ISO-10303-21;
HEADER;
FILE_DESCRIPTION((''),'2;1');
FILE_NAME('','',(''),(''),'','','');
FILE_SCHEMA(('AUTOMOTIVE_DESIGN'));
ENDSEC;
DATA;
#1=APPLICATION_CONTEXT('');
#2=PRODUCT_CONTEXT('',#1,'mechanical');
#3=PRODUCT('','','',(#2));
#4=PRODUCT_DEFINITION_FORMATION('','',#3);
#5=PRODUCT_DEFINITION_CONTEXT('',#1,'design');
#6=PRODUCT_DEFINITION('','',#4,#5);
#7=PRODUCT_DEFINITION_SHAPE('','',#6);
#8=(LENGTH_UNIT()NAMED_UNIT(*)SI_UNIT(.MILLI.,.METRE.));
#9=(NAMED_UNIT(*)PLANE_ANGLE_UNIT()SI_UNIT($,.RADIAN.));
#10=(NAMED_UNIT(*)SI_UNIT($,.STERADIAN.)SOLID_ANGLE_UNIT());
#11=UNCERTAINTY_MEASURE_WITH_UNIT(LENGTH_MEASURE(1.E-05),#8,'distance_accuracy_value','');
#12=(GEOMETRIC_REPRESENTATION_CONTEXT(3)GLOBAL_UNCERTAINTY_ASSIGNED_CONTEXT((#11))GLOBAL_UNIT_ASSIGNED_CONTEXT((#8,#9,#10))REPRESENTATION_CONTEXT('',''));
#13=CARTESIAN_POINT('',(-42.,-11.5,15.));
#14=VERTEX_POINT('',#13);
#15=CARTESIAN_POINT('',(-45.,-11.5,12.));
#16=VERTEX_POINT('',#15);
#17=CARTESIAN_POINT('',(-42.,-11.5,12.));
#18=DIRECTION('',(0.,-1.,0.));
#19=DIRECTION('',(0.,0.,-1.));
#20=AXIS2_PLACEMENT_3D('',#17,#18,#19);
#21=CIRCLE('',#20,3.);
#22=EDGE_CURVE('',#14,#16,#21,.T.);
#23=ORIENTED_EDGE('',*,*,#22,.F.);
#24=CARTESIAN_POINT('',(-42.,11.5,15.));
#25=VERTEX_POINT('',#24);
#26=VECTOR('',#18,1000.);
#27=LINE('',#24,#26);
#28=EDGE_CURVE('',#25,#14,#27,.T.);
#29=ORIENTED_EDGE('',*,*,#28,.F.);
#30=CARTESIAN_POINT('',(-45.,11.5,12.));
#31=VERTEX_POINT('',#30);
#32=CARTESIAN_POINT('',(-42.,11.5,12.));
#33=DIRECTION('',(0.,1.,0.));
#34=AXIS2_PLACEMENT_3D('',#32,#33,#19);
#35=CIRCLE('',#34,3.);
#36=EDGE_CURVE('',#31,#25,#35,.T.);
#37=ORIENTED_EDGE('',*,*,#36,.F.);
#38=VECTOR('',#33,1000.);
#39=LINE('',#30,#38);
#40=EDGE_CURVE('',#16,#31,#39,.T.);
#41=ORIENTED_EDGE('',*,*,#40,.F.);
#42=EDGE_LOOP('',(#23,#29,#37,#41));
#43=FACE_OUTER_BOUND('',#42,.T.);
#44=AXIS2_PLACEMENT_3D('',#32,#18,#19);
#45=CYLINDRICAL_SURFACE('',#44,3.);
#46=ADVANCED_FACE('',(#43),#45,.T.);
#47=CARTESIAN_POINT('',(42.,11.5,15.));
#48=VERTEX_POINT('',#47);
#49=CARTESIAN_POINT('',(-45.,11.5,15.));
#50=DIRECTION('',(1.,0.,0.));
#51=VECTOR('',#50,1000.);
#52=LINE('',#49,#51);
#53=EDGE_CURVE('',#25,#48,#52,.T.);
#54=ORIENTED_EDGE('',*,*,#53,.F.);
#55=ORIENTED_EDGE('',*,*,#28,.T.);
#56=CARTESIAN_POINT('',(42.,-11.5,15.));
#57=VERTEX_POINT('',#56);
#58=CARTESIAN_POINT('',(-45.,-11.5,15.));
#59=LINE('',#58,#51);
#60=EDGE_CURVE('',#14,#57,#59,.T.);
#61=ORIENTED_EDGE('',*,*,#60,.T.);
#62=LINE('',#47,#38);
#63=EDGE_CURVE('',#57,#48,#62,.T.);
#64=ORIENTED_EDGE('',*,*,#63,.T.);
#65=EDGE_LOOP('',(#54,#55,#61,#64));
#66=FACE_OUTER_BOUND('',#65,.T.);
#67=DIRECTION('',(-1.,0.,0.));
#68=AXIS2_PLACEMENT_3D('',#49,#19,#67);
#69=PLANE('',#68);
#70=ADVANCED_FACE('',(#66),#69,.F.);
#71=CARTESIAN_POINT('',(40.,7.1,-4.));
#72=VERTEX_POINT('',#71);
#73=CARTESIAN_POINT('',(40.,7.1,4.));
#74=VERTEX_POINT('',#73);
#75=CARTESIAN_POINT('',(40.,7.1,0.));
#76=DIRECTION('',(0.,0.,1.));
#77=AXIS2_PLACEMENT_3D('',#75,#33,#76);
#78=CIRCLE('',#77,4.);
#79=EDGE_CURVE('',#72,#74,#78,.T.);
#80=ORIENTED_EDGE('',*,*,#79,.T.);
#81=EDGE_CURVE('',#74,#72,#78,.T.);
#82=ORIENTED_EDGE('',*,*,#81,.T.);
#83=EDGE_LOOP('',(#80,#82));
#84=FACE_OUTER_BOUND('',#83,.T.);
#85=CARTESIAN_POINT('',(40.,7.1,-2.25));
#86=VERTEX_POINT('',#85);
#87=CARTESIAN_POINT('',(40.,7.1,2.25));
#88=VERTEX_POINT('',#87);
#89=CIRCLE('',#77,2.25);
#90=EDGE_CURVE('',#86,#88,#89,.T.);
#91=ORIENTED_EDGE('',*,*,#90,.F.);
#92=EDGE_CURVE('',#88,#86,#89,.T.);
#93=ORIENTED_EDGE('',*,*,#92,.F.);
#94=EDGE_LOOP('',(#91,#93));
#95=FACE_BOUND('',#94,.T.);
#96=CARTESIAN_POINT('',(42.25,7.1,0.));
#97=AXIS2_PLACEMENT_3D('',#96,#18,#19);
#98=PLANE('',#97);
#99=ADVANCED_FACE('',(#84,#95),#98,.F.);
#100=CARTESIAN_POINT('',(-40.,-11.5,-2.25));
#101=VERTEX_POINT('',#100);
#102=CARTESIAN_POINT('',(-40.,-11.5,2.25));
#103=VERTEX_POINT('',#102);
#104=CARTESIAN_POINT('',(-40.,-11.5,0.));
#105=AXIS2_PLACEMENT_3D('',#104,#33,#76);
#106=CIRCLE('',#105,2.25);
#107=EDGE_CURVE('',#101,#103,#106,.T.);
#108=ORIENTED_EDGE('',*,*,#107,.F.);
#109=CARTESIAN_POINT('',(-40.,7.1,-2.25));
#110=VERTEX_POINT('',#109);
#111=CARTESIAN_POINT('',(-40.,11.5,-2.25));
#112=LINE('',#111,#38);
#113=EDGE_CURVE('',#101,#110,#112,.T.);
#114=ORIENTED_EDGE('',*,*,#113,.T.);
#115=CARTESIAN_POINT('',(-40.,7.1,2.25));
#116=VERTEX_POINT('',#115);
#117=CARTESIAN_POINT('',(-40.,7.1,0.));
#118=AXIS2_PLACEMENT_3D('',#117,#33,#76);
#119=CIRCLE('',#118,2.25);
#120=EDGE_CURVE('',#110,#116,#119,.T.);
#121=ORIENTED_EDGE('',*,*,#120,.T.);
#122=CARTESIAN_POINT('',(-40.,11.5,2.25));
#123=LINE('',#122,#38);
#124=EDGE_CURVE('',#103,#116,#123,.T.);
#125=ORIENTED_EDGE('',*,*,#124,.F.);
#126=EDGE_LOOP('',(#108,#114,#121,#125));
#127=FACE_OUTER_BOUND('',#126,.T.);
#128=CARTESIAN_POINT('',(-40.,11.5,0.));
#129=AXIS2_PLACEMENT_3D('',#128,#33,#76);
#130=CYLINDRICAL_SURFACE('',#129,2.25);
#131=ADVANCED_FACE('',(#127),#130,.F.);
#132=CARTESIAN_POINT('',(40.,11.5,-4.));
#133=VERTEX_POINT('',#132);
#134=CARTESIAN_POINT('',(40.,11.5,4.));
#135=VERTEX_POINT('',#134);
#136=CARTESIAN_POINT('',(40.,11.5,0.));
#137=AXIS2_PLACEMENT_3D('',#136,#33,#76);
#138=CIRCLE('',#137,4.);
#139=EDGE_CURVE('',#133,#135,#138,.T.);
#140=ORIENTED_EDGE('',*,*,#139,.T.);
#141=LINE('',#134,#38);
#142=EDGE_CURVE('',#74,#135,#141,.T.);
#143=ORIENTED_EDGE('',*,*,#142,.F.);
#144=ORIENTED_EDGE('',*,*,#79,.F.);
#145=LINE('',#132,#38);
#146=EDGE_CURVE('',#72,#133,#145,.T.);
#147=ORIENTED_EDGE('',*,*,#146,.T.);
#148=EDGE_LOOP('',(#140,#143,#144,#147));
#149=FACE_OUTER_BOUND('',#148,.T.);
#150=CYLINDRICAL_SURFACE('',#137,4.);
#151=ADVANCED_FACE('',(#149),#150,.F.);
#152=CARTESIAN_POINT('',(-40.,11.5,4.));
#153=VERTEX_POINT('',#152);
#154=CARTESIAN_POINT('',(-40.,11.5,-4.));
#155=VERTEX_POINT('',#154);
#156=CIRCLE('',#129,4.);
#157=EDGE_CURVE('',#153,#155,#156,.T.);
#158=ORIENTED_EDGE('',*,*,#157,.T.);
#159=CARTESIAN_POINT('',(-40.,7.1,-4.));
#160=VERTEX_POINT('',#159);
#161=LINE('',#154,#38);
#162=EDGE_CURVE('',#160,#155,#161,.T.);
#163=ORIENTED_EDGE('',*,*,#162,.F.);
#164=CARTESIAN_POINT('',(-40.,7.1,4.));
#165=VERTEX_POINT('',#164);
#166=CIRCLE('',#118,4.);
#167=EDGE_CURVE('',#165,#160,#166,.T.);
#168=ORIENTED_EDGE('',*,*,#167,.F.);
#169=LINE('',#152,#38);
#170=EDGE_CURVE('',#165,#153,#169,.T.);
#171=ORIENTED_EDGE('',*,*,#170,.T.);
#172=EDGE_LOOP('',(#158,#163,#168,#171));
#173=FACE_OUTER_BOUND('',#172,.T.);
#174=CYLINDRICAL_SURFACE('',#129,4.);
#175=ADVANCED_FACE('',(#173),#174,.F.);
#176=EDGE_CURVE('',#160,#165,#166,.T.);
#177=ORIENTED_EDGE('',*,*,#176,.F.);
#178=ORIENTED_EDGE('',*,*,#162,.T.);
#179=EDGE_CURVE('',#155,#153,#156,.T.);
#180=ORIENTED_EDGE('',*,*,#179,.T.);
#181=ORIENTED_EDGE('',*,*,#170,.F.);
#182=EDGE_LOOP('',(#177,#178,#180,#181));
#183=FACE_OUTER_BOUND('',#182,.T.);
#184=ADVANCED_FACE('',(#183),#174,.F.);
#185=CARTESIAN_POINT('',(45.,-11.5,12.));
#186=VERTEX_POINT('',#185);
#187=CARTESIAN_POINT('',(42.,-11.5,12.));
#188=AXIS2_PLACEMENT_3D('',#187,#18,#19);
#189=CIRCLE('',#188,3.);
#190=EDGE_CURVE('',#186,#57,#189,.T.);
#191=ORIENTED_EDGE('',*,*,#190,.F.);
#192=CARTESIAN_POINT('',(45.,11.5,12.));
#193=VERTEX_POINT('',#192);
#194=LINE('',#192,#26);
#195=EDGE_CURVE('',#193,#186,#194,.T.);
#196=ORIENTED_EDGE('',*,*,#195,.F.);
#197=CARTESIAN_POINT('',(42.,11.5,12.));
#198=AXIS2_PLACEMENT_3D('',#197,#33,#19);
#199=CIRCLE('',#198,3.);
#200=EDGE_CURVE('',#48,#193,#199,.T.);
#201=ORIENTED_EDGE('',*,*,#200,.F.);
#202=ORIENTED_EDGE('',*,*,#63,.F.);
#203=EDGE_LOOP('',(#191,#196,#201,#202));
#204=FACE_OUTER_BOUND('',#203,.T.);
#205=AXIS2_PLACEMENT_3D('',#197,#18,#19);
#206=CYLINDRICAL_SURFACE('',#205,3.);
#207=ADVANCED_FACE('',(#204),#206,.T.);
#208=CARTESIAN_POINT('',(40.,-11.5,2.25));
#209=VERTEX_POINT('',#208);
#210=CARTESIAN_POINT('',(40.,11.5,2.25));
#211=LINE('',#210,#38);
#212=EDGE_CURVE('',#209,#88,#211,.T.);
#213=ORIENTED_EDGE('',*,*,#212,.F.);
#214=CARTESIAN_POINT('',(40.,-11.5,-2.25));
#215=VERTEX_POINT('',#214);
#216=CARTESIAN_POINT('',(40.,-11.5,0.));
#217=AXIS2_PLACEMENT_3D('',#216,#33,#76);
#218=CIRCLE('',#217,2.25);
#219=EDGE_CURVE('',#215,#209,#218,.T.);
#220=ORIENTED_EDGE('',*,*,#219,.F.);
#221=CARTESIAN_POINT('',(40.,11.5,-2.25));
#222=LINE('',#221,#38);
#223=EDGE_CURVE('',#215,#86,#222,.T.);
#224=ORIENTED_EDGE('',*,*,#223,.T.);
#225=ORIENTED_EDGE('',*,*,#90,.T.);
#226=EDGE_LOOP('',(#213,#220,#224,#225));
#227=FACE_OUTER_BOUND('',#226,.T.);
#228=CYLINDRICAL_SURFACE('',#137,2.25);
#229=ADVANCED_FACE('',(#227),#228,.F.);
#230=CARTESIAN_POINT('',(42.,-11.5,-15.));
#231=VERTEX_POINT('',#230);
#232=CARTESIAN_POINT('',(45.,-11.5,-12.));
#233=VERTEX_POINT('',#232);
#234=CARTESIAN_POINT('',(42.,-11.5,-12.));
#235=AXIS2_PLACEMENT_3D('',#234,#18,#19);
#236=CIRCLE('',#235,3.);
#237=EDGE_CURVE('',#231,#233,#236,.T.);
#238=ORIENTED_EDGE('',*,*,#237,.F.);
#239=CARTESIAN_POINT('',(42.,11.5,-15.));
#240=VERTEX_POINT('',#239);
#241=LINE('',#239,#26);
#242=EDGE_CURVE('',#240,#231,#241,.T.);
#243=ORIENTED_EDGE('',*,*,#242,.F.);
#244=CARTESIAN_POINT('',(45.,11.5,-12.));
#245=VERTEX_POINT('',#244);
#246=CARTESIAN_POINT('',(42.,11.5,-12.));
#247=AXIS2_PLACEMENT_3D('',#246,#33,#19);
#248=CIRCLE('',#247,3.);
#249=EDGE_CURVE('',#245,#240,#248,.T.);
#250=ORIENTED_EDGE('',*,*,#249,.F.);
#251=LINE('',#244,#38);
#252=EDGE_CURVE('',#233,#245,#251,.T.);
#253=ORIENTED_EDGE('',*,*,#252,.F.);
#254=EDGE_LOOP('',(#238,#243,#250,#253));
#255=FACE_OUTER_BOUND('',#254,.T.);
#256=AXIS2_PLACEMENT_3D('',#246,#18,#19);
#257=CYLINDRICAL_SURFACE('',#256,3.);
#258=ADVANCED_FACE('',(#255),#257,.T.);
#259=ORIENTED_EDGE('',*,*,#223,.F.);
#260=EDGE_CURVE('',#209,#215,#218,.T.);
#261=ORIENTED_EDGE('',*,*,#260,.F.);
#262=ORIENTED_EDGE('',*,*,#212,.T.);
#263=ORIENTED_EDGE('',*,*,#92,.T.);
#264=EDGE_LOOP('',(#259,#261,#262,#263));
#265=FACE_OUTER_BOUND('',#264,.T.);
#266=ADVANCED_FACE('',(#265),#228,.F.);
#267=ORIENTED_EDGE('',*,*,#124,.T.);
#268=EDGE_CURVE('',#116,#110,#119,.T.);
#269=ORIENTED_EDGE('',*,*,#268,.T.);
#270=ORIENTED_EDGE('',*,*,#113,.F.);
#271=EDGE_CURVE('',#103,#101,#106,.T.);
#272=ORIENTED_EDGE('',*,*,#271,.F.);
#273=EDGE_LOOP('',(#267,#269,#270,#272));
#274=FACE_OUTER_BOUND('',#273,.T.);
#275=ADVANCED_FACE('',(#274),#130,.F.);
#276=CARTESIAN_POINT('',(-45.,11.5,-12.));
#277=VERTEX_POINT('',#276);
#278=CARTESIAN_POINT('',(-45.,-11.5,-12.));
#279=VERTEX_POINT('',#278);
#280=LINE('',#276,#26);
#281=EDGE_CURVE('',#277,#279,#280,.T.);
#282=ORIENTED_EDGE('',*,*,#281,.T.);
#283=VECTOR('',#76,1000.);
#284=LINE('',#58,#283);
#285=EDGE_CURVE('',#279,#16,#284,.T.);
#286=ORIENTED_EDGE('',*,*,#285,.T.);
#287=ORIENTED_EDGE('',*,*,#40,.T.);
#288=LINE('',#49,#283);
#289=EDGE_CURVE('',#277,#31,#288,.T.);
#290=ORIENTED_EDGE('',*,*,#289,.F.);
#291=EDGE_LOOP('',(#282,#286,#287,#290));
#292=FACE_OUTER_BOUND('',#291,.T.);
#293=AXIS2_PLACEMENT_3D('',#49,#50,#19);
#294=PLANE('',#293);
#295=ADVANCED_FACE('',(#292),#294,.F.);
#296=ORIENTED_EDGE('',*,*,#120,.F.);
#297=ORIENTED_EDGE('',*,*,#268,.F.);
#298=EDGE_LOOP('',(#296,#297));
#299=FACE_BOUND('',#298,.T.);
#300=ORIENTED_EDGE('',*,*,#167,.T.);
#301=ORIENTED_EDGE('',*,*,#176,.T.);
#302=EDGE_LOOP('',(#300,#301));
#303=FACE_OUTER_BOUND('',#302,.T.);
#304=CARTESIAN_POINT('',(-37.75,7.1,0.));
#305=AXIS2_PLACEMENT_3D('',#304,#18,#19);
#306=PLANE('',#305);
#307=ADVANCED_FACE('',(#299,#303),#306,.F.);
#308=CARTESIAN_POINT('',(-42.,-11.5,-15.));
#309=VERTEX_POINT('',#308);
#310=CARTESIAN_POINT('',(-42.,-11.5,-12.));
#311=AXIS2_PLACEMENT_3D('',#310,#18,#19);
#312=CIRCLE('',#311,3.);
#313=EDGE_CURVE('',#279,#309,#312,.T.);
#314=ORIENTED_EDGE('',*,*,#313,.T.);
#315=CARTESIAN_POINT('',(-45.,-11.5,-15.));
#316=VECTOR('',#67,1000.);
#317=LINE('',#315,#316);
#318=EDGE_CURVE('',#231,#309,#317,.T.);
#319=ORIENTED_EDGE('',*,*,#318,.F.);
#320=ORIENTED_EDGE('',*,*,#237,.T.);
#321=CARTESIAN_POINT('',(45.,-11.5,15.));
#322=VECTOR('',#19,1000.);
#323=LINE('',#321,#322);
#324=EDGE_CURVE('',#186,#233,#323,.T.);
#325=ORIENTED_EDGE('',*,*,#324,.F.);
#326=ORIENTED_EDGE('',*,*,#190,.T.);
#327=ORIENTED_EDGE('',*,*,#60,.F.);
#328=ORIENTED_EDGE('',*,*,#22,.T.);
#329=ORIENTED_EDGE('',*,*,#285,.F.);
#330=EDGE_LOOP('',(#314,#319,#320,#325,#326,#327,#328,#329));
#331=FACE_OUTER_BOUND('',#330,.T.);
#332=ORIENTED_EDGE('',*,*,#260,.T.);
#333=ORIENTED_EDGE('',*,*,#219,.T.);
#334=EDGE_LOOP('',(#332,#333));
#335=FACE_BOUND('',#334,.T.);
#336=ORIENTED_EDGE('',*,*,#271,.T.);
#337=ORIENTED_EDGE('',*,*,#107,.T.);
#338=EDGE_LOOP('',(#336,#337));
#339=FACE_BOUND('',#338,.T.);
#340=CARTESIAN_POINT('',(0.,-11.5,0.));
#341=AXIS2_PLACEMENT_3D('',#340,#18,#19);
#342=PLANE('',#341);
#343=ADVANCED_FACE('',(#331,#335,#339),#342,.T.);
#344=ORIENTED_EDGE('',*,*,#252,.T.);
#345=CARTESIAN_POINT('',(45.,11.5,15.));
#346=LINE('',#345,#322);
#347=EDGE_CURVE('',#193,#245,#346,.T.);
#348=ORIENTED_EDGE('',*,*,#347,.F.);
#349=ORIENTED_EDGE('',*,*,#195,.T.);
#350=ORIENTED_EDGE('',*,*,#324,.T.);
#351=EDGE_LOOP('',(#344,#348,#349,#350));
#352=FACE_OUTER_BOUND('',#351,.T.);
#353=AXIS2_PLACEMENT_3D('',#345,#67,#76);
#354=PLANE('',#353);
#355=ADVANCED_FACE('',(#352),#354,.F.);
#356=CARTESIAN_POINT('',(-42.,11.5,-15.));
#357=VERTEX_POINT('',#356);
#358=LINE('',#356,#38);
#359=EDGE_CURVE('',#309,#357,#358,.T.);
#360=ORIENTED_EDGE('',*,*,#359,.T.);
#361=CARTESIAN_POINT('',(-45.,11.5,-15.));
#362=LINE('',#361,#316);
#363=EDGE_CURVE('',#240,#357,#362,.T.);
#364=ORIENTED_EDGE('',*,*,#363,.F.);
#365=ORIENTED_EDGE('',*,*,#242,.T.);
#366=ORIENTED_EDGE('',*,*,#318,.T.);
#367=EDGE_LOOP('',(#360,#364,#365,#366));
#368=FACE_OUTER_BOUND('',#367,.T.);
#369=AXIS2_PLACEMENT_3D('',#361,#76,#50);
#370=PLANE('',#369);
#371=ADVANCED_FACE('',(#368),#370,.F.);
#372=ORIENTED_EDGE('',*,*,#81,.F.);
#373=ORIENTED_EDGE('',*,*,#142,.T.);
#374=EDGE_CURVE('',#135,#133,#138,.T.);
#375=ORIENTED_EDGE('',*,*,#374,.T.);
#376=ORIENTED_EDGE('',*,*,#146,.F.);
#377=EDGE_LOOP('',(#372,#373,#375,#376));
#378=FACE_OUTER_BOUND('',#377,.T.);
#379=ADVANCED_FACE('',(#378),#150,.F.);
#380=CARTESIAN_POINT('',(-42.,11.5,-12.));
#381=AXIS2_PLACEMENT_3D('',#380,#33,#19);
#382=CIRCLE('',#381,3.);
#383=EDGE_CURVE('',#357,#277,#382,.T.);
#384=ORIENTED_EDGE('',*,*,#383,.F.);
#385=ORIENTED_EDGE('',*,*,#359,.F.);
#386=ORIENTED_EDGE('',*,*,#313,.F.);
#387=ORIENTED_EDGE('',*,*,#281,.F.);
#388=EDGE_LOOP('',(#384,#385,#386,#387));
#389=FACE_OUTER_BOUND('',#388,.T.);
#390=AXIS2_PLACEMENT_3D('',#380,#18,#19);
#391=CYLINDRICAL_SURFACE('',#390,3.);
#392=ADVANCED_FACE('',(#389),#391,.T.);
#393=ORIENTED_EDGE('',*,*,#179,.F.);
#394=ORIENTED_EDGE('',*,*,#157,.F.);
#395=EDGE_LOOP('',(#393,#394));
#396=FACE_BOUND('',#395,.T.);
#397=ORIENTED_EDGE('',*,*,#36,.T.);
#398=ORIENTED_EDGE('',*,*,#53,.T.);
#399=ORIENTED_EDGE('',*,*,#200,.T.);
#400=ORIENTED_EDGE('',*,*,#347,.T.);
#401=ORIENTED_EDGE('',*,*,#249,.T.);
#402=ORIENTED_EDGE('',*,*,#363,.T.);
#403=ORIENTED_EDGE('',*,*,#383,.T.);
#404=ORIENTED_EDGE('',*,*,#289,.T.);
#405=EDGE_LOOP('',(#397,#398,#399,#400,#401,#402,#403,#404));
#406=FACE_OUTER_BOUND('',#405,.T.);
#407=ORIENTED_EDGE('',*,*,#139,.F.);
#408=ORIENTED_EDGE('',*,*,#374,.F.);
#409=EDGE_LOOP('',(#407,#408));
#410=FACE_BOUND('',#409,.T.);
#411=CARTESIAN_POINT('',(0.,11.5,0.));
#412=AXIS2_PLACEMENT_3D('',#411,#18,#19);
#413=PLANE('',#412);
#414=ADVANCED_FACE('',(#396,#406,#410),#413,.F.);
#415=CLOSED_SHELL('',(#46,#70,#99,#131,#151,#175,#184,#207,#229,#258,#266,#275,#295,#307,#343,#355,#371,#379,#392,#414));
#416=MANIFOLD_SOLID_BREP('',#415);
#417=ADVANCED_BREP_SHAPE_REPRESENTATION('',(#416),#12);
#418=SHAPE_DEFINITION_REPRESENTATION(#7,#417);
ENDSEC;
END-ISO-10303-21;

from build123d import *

# Parameters (mm, degrees)
SKETCH_1_W                   = 90
SKETCH_1_H                   = 30
EXTRUDE_1_DEPTH              = 11.5
HOLE_WIZARD_M4_1_D           = 4.5
HOLE_WIZARD_M4_1_CBORE_D     = 8
HOLE_WIZARD_M4_1_CBORE_DEPTH = 4.4
FILLET_1_R                   = 3


with BuildPart() as part:
    # 草图1 → 凸台-拉伸1 (new, symmetric)
    with BuildSketch(Plane(origin=(0, 0, 0), x_dir=(1, 0, 0), z_dir=(0, 1, 0))):
        Rectangle(SKETCH_1_W, SKETCH_1_H)
    extrude(amount=EXTRUDE_1_DEPTH, both=True)

    # M4 六角凹头螺钉的柱形沉头孔1 (through all)
    with Locations(Plane(origin=(0, 11.5, 0), x_dir=(1, 0, 0), z_dir=(0, 1, 0))):
        with Locations((-40, 0), (40, 0)):
            CounterBoreHole(HOLE_WIZARD_M4_1_D / 2, HOLE_WIZARD_M4_1_CBORE_D / 2, HOLE_WIZARD_M4_1_CBORE_DEPTH)

    # 圆角1
    fillet_1_edges = [part.edges().sort_by_distance(p)[0] for p in [
        (45, 0, 15),
        (-45, 0, 15),
        (-45, 0, -15),
        (45, 0, -15),
    ]]
    fillet(fillet_1_edges, radius=FILLET_1_R)


solid = part.part
